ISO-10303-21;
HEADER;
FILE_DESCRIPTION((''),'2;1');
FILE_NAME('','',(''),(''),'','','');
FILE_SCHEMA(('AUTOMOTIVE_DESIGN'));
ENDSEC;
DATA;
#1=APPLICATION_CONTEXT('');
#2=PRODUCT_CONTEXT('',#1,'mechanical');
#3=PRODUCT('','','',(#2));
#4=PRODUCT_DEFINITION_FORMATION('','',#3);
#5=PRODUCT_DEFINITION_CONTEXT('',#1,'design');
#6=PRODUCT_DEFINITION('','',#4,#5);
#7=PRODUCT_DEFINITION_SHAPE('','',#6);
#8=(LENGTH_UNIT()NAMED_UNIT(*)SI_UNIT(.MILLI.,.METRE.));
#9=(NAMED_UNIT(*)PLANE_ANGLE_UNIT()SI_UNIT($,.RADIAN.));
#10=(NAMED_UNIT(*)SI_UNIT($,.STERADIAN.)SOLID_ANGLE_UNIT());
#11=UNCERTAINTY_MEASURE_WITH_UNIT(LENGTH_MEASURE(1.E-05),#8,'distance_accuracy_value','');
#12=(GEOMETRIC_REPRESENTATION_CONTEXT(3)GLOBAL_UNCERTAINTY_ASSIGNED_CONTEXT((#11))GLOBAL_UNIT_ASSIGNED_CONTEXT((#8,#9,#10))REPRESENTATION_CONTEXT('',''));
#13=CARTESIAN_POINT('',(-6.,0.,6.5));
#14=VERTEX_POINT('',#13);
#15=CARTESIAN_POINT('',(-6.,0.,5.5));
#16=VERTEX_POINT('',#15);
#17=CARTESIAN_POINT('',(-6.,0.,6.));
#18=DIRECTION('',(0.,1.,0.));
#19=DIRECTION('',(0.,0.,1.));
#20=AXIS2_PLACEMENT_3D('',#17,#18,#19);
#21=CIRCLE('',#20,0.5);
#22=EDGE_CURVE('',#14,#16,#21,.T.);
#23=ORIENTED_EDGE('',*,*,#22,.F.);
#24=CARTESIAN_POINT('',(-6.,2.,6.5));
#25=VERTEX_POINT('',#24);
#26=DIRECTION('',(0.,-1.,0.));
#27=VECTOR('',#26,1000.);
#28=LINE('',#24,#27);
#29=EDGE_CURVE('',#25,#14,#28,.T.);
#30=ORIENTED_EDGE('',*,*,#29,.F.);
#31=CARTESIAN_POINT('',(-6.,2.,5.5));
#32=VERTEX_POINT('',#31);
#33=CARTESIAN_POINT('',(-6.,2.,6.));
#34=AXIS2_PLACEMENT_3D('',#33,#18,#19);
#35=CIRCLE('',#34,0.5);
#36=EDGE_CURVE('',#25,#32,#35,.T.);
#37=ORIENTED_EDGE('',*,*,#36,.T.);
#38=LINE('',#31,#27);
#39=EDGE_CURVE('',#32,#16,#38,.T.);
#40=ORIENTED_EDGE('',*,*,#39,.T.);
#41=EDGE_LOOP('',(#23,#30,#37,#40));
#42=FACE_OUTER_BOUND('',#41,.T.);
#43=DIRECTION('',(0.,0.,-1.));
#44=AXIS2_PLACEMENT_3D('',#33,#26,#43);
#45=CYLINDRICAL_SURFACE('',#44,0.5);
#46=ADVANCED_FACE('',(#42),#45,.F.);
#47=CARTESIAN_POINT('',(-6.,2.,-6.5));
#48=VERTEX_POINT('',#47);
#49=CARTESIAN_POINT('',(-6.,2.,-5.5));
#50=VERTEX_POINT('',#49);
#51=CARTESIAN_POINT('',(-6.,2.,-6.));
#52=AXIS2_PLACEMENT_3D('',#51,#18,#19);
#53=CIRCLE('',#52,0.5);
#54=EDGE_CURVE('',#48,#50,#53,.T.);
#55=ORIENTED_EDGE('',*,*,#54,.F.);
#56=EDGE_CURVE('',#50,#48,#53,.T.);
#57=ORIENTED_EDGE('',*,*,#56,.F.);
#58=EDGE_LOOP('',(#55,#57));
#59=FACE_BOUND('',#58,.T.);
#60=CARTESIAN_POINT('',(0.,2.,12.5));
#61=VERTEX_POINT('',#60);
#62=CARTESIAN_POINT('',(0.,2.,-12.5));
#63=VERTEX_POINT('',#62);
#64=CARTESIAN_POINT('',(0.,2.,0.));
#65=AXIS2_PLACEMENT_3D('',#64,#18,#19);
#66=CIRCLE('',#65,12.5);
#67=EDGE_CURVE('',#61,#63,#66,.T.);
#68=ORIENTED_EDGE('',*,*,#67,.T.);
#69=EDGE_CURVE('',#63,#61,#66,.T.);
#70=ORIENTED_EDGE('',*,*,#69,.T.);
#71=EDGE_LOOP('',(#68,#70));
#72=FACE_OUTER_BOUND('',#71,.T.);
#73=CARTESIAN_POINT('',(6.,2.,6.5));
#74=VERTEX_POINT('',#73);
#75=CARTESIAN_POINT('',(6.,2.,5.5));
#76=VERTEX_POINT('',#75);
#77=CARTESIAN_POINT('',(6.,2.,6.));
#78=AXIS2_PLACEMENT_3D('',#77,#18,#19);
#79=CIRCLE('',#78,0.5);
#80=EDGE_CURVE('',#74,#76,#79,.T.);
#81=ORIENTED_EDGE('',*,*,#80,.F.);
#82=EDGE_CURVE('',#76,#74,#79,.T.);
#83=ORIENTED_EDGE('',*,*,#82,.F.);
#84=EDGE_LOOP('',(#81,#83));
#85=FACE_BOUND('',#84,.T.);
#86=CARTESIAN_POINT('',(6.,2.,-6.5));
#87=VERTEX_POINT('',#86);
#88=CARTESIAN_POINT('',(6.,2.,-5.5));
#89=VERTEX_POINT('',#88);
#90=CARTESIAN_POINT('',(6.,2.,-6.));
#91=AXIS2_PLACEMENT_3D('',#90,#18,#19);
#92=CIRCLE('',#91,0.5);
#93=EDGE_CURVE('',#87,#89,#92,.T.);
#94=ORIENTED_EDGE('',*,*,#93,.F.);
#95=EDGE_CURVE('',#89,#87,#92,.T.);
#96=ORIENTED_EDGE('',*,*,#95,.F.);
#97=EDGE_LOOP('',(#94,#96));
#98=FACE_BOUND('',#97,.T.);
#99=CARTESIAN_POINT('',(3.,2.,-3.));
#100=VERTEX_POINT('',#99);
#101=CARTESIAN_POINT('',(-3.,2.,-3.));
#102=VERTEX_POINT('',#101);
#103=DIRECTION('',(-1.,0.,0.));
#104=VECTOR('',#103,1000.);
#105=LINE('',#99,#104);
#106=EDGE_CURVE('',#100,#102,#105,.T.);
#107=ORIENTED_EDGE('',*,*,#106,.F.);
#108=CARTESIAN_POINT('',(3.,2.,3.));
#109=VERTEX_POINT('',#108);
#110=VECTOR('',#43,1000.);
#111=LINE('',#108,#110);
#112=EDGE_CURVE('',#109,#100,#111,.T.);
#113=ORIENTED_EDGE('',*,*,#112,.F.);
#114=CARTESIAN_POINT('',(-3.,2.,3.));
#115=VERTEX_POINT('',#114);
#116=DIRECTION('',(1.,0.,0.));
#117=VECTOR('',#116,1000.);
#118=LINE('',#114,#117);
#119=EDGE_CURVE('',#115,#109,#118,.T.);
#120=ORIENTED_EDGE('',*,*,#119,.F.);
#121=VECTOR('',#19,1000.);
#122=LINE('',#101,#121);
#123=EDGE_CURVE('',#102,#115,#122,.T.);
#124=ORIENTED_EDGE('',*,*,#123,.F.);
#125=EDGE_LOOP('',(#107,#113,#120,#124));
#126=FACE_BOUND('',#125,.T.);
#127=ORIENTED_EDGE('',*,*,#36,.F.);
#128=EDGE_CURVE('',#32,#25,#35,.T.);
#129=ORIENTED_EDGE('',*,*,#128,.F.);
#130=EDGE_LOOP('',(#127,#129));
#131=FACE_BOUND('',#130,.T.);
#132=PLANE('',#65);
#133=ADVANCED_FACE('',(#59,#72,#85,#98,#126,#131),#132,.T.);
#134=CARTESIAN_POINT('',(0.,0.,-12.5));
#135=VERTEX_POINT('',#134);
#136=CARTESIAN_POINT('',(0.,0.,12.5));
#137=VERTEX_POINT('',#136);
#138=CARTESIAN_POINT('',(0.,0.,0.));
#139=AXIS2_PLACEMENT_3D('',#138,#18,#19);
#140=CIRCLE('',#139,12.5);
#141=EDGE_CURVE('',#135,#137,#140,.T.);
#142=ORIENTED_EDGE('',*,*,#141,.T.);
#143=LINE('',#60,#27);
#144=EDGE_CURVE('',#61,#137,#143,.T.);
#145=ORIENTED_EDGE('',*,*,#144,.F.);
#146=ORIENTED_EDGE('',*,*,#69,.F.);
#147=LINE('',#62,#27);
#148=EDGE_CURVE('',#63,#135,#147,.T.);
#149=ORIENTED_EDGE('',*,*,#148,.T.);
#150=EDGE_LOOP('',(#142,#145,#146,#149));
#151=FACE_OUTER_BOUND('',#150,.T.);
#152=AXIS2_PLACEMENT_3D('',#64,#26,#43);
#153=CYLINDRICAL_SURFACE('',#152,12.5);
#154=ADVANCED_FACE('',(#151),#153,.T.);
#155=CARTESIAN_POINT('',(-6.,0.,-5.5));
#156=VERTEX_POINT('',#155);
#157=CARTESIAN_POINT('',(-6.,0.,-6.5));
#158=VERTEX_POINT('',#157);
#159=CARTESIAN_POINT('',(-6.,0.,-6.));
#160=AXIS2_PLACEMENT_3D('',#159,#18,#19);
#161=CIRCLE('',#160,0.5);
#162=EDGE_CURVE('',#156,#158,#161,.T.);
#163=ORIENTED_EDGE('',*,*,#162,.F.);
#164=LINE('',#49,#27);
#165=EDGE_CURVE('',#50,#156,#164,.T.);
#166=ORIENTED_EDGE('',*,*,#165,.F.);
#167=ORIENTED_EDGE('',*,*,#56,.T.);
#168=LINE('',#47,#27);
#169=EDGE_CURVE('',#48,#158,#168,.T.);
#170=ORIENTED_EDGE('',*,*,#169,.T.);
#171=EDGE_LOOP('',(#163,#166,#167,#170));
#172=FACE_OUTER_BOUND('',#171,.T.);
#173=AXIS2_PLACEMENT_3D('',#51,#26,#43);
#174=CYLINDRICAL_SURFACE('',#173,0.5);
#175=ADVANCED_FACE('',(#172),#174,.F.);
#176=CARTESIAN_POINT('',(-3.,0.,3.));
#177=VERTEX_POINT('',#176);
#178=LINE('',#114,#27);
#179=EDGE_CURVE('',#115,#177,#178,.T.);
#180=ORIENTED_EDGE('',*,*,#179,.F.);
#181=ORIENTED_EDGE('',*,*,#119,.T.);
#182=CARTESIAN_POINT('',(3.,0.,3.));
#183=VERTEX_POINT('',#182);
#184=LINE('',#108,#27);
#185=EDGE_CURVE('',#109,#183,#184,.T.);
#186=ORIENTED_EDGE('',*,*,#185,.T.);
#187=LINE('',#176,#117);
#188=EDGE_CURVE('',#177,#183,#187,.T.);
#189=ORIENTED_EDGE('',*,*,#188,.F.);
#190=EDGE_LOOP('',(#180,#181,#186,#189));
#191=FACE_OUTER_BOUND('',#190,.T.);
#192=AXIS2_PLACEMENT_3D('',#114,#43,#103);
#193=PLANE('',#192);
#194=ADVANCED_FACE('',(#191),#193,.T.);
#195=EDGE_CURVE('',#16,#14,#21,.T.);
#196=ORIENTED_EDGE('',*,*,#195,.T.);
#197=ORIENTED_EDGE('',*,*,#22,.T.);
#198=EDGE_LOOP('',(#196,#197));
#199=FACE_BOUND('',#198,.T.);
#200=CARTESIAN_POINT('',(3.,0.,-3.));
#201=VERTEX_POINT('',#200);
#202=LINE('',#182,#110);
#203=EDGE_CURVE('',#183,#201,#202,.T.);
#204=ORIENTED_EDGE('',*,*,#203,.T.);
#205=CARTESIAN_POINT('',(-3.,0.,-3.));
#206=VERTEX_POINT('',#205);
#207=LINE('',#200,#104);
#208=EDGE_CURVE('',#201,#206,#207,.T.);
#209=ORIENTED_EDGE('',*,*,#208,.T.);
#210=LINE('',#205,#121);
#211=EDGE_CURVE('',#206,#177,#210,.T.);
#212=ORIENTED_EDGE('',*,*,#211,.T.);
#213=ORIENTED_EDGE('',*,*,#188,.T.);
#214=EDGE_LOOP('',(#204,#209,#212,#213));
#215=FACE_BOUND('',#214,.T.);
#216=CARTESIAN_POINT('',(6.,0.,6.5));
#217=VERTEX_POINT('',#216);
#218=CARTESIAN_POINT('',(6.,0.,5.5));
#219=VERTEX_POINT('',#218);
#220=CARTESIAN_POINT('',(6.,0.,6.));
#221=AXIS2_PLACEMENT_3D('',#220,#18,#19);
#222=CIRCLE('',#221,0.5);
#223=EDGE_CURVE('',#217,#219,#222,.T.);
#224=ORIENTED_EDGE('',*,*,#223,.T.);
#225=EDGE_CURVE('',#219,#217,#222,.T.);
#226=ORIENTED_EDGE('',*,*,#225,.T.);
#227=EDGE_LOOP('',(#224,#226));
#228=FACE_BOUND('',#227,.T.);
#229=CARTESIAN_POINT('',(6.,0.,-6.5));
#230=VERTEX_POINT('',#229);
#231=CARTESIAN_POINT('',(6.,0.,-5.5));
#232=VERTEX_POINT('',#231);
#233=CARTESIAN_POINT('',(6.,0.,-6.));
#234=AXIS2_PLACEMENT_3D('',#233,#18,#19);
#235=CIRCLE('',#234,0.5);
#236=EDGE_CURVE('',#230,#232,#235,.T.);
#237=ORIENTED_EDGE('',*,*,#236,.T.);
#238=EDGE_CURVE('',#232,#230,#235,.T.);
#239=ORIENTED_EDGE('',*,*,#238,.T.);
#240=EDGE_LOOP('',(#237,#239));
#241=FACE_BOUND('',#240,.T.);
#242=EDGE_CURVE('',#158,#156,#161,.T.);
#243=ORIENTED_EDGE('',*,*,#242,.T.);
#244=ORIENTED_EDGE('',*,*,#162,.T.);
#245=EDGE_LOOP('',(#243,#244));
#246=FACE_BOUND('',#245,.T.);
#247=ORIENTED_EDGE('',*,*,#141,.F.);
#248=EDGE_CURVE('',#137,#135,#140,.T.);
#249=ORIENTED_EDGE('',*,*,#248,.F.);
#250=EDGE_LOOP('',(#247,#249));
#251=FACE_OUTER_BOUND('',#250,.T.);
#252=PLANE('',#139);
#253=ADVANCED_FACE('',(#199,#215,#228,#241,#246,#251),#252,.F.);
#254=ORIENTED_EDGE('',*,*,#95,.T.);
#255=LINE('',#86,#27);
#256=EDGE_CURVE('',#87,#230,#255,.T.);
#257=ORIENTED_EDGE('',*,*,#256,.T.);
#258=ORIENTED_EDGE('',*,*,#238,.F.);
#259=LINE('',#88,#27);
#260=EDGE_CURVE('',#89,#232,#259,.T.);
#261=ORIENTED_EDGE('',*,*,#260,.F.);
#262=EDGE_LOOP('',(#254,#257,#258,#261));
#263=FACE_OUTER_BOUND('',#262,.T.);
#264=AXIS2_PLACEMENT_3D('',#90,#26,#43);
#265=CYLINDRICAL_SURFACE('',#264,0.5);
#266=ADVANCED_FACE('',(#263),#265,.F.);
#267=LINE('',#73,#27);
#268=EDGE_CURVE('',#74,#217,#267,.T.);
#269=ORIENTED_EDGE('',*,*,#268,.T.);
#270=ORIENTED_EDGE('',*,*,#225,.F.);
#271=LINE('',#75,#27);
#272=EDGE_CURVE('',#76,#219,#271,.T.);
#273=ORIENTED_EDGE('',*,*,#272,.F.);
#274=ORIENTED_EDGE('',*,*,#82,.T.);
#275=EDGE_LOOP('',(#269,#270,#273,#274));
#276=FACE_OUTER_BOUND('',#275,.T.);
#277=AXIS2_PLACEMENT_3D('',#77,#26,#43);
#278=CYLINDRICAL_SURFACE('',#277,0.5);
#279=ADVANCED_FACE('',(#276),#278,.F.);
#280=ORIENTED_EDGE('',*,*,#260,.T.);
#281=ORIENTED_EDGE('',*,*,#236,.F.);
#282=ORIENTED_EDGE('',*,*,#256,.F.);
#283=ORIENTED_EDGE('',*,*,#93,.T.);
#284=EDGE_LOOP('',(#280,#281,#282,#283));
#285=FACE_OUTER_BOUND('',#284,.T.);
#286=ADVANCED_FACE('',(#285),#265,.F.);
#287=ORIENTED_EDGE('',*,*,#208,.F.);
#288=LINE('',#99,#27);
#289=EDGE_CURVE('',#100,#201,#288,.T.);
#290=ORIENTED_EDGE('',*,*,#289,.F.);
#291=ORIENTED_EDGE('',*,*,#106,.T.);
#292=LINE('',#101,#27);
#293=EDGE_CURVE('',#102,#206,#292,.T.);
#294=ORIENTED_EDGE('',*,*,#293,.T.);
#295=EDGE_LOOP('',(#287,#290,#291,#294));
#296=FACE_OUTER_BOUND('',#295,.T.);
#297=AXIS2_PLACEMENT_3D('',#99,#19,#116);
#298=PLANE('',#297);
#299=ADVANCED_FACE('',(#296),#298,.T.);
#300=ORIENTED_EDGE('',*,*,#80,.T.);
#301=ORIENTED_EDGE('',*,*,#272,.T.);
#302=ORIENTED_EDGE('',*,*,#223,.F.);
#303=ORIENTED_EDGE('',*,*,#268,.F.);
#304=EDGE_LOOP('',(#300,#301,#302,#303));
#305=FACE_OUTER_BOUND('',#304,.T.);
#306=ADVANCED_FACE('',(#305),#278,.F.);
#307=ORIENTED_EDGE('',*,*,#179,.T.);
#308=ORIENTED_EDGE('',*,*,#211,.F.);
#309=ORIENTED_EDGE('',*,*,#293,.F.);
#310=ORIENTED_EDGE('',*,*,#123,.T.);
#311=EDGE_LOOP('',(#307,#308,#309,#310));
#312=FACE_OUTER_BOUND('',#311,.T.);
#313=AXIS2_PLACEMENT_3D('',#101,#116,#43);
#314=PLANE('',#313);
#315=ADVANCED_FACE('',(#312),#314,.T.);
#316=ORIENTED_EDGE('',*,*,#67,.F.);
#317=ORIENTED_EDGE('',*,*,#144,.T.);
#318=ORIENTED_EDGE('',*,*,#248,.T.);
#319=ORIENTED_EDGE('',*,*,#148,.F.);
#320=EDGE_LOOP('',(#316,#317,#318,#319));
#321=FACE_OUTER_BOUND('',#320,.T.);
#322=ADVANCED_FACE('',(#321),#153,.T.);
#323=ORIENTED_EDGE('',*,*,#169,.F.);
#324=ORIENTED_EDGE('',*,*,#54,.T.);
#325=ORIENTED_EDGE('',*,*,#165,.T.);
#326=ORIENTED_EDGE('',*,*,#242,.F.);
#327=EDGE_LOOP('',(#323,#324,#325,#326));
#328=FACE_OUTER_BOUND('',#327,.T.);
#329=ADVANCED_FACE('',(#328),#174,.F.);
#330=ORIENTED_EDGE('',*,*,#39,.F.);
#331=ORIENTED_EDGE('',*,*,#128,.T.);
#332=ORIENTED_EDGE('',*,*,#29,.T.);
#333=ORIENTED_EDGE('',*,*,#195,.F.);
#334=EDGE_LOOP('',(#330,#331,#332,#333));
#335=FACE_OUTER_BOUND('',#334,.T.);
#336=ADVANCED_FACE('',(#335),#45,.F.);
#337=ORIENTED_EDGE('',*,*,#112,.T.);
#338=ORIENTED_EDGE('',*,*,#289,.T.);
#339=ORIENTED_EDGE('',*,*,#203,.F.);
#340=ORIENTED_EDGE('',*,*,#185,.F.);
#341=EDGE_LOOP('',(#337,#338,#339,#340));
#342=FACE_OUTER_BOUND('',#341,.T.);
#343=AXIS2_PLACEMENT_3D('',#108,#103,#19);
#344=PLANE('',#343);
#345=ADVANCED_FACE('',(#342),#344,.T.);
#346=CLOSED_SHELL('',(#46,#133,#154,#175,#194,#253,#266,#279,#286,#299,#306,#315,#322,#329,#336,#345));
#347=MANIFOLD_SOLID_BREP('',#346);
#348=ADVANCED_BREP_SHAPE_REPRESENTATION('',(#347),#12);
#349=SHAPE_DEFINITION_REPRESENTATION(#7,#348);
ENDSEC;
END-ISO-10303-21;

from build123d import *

# Parameters (mm, degrees)
SKETCH1_R           = 12.5
SKETCH1_R_2         = 0.5
SKETCH1_W           = 6
SKETCH1_H           = 6
BOSS_EXTRUDE1_DEPTH = 2


with BuildPart() as part:
    # Sketch1 → Boss-Extrude1 (new body)
    with BuildSketch(Plane(origin=(0, 0, 0), x_dir=(1, 0, 0), z_dir=(0, 1, 0))):
        with Locations(Location((0, 0, 0), (0, 0, 270))):
            Circle(SKETCH1_R)
        with Locations(Location((-6, 6, 0), (0, 0, 270))):
            Circle(SKETCH1_R_2, mode=Mode.SUBTRACT)
        with Locations(Location((6, 6, 0), (0, 0, 270))):
            Circle(SKETCH1_R_2, mode=Mode.SUBTRACT)
        with Locations(Location((-6, -6, 0), (0, 0, 270))):
            Circle(SKETCH1_R_2, mode=Mode.SUBTRACT)
        with Locations(Location((6, -6, 0), (0, 0, 270))):
            Circle(SKETCH1_R_2, mode=Mode.SUBTRACT)
        Rectangle(SKETCH1_W, SKETCH1_H, mode=Mode.SUBTRACT)
    extrude(amount=BOSS_EXTRUDE1_DEPTH)


solid = part.part
